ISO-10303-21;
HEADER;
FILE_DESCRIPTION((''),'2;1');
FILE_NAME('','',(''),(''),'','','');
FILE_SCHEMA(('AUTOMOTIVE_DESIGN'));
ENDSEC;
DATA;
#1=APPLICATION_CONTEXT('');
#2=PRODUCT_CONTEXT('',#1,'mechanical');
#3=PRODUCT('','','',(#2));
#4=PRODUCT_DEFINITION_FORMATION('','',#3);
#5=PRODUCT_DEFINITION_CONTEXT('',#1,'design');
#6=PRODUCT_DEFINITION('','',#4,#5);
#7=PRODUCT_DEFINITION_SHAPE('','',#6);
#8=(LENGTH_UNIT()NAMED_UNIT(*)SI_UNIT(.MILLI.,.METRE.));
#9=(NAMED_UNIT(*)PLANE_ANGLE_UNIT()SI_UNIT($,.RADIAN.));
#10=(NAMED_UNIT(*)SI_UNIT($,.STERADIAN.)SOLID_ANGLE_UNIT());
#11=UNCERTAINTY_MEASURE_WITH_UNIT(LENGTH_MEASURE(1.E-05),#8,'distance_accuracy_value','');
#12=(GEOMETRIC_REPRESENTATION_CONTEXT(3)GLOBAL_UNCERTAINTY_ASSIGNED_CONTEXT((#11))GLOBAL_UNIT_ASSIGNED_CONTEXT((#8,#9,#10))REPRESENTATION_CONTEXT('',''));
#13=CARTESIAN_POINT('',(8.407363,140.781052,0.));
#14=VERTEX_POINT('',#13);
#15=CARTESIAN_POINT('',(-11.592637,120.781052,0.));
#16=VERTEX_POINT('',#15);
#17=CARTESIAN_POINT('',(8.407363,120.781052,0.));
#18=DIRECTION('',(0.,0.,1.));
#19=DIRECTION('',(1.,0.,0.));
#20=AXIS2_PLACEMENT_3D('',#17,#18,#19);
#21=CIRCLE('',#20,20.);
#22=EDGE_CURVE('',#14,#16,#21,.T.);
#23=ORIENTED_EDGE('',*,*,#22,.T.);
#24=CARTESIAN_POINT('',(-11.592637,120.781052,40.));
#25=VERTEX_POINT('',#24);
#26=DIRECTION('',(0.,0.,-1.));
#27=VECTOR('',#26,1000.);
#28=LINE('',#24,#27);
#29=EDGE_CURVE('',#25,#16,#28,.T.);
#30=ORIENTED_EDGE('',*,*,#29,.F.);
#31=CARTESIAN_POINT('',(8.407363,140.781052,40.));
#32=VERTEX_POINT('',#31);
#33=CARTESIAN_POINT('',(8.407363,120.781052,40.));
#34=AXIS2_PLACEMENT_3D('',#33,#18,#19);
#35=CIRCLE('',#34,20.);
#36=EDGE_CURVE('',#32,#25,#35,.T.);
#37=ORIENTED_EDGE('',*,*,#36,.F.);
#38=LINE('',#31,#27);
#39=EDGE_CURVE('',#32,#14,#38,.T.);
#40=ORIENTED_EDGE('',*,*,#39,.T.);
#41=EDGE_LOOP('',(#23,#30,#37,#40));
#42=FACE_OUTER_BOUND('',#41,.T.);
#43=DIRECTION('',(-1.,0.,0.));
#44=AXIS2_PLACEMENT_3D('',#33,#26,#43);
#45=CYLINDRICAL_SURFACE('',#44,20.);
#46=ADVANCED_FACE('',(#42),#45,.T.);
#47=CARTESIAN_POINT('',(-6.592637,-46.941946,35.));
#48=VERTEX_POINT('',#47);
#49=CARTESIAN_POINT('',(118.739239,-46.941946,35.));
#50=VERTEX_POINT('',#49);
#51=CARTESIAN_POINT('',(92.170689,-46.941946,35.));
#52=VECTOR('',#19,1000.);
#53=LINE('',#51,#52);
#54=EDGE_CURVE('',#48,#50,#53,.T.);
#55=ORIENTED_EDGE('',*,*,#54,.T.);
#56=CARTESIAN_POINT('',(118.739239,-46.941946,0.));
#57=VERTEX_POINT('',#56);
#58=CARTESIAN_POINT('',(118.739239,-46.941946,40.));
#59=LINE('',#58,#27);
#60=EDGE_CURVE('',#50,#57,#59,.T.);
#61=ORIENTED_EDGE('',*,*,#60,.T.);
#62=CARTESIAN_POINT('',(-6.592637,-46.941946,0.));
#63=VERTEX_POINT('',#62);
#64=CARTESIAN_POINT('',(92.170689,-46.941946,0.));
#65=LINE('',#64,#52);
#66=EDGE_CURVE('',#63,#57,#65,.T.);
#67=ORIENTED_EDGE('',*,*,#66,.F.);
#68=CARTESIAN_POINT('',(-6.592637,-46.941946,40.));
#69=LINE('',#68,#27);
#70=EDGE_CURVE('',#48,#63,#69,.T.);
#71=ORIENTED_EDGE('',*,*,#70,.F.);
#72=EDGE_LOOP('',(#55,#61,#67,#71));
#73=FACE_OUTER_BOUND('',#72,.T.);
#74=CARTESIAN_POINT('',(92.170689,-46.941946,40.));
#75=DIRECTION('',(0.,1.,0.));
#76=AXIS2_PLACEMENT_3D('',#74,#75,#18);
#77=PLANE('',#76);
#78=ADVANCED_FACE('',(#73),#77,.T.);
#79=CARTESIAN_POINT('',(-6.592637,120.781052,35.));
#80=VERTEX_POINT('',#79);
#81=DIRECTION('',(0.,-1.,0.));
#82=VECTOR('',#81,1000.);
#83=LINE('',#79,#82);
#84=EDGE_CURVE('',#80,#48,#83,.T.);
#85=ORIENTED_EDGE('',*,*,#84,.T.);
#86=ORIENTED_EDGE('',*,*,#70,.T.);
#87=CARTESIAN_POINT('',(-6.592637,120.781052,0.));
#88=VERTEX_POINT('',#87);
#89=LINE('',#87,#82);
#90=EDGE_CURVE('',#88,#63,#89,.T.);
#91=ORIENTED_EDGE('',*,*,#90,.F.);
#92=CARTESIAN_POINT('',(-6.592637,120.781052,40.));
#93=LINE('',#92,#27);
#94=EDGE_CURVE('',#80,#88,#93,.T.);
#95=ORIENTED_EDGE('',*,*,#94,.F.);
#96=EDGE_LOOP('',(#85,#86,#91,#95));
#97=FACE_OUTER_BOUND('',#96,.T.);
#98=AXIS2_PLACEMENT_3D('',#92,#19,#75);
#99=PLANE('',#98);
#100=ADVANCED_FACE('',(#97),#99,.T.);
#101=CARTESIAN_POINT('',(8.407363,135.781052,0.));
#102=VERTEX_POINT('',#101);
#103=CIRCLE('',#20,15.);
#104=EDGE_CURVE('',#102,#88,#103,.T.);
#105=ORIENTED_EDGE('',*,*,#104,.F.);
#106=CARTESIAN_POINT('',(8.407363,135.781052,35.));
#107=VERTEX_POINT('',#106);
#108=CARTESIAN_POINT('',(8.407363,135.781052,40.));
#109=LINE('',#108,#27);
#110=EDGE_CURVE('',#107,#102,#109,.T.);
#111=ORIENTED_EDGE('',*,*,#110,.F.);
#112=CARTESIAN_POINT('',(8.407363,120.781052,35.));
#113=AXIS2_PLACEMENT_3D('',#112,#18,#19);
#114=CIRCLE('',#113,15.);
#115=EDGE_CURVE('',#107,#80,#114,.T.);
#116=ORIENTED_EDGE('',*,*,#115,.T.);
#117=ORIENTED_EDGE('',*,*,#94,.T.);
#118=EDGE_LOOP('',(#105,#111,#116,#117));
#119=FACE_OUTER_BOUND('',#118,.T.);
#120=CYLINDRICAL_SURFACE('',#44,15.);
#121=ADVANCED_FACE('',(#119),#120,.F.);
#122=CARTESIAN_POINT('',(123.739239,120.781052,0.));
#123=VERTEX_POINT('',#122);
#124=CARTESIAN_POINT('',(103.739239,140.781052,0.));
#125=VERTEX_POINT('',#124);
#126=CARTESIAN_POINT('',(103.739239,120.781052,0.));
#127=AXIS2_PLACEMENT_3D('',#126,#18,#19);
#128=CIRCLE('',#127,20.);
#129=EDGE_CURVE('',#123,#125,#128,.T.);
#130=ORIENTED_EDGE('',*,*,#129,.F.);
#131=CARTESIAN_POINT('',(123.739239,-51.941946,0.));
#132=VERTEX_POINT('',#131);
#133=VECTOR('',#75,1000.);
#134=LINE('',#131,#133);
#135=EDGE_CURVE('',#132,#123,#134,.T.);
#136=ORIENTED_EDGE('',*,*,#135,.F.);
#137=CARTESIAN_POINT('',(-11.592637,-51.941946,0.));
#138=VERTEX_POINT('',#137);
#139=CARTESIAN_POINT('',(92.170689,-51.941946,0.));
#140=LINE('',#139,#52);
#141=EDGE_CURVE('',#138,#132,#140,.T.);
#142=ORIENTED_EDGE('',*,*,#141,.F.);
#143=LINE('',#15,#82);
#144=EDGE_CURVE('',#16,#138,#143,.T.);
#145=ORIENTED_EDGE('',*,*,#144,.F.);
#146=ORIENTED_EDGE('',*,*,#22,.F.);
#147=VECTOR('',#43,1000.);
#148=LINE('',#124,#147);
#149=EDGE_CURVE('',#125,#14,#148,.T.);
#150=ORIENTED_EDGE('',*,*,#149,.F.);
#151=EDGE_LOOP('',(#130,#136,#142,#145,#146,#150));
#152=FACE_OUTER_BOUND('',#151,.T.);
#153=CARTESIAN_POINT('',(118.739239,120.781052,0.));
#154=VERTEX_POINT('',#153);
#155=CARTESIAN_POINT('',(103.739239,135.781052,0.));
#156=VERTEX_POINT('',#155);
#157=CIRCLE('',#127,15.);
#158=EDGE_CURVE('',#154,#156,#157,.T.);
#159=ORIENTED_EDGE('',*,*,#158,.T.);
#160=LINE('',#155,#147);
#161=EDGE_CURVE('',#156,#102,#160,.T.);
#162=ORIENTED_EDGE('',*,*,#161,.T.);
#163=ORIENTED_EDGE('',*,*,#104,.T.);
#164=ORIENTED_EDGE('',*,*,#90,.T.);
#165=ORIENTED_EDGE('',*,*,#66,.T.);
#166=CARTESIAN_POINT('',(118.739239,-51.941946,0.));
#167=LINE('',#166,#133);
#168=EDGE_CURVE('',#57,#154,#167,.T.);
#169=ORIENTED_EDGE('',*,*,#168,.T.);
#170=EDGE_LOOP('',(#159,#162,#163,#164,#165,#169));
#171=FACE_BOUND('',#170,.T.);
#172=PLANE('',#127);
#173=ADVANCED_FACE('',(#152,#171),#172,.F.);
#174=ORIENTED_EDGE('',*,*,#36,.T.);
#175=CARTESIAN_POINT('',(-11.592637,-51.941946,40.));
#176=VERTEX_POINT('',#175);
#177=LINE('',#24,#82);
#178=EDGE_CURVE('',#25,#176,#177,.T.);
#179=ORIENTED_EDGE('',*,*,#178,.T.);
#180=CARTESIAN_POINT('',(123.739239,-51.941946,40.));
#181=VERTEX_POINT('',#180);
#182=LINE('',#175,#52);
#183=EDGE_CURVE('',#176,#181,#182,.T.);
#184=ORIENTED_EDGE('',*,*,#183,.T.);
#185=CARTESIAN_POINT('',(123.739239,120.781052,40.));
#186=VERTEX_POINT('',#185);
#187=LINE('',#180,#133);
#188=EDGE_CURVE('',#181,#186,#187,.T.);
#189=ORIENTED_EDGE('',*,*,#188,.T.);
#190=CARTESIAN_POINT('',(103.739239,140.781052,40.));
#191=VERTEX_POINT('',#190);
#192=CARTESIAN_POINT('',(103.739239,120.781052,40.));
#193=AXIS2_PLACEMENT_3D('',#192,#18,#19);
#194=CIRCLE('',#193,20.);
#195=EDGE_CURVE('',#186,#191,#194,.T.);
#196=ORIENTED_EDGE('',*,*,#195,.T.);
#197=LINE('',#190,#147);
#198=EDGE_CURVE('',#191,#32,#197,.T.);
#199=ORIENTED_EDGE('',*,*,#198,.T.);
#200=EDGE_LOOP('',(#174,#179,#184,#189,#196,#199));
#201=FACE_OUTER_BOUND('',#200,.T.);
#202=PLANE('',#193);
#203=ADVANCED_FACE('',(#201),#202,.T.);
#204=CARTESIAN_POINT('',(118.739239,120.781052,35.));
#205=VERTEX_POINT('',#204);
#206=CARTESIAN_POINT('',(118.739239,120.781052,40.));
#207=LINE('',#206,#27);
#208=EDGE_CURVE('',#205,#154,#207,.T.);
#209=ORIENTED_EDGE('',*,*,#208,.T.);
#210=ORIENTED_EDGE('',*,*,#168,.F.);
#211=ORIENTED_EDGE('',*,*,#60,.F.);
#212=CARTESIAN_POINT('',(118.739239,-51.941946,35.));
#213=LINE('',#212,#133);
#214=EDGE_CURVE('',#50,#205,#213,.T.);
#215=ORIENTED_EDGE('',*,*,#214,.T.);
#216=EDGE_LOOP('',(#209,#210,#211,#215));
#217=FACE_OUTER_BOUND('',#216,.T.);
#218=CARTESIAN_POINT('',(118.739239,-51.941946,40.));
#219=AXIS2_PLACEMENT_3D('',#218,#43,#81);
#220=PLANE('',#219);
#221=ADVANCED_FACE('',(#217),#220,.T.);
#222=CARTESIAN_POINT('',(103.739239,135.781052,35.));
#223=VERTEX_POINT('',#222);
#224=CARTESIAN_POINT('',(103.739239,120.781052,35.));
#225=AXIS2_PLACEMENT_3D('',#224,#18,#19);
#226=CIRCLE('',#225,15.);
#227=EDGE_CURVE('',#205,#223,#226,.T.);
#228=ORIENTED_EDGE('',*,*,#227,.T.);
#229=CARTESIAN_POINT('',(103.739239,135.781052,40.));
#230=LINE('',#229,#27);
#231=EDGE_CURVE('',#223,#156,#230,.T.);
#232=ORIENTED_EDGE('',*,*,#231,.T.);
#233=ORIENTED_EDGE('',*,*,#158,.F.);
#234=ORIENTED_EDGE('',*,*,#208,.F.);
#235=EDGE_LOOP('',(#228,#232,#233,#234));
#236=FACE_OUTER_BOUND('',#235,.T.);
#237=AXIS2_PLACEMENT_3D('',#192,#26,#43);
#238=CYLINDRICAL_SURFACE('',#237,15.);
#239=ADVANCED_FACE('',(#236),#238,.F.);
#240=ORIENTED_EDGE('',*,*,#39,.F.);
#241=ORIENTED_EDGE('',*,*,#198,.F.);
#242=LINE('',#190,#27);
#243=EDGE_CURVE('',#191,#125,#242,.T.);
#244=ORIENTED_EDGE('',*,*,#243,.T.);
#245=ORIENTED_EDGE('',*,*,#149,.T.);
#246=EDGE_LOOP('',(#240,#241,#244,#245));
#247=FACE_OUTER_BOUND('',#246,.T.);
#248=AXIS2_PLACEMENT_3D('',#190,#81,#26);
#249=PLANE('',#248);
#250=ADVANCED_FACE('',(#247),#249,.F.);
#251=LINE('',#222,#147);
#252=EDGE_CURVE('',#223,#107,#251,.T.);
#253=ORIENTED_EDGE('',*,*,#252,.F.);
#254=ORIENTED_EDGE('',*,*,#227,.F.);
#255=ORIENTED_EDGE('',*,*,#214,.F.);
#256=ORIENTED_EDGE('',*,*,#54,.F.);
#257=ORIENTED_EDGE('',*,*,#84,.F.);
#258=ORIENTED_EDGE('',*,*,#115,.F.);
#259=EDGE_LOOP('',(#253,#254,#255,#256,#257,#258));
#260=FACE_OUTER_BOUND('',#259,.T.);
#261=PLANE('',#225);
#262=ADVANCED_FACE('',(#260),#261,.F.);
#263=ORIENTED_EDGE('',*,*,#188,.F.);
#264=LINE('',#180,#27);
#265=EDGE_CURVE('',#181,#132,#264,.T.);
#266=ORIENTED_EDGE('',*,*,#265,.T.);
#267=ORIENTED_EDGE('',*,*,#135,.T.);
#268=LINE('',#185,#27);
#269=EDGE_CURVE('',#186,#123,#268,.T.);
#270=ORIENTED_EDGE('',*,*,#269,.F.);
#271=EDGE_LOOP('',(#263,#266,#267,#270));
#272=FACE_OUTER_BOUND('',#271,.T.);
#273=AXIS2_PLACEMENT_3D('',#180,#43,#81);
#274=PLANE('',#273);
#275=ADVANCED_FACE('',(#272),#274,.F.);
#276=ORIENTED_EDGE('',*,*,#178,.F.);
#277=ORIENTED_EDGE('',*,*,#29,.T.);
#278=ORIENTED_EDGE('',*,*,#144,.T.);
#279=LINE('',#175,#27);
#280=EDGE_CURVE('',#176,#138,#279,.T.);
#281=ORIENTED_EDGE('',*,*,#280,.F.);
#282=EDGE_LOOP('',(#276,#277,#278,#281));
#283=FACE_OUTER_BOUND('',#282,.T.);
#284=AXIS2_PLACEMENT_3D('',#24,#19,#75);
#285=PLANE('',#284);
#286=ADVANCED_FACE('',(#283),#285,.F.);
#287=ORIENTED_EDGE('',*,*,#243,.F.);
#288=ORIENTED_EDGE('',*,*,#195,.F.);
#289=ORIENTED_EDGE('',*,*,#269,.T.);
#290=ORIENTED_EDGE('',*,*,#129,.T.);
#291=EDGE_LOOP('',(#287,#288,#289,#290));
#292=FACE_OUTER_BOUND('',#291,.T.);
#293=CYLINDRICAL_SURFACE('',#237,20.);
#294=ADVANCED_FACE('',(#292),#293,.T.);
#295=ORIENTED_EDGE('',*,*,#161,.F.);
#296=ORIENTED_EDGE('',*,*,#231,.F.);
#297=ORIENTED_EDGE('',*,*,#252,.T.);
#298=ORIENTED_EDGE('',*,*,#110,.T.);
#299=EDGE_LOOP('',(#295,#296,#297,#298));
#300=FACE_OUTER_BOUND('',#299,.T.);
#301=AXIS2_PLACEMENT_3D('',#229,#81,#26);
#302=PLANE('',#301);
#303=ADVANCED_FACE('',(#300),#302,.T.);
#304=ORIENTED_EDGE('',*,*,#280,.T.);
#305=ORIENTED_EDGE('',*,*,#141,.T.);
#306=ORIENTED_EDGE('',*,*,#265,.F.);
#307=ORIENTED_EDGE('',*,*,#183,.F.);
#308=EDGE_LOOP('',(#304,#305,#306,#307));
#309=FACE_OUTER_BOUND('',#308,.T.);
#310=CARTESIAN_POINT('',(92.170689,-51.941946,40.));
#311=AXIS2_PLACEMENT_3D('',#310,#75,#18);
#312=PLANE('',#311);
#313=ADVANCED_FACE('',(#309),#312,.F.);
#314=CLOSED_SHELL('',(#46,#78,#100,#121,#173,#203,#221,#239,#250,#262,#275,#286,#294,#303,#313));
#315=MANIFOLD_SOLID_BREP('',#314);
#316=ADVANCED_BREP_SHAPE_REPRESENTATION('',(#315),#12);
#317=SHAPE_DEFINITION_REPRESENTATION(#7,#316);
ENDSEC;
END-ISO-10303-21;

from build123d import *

# Parameters (mm, degrees)
BOSS_EXTRUDE1_DEPTH = 40
SHELL1_T            = -5


with BuildPart() as part:
    # Sketch1 → Boss-Extrude1 (new body)
    with BuildSketch(Plane.XY):
        with BuildLine():
            Line((-11.59263729, -51.941945741), (92.170688637, -51.941945741))
            Line((92.170688637, -51.941945741), (123.739238561, -51.941945741))
            Line((123.739238561, -51.941945741), (123.739238561, 120.781051565))
            ThreePointArc((123.739238561, 120.781051565), (117.881374185, 134.923187188), (103.739238561, 140.781051565))
            Line((103.739238561, 140.781051565), (8.40736271, 140.781051565))
            ThreePointArc((8.40736271, 140.781051565), (-5.734772914, 134.923187188), (-11.59263729, 120.781051565))
            Line((-11.59263729, 120.781051565), (-11.59263729, -51.941945741))
        make_face()
    extrude(amount=BOSS_EXTRUDE1_DEPTH)

    # Shell1
    shell1_openings = [part.faces().sort_by_distance(p)[0] for p in [
        (56.073300636, 43.810653181, 0),
    ]]
    offset(amount=SHELL1_T, openings=shell1_openings, kind=Kind.INTERSECTION)


solid = part.part
